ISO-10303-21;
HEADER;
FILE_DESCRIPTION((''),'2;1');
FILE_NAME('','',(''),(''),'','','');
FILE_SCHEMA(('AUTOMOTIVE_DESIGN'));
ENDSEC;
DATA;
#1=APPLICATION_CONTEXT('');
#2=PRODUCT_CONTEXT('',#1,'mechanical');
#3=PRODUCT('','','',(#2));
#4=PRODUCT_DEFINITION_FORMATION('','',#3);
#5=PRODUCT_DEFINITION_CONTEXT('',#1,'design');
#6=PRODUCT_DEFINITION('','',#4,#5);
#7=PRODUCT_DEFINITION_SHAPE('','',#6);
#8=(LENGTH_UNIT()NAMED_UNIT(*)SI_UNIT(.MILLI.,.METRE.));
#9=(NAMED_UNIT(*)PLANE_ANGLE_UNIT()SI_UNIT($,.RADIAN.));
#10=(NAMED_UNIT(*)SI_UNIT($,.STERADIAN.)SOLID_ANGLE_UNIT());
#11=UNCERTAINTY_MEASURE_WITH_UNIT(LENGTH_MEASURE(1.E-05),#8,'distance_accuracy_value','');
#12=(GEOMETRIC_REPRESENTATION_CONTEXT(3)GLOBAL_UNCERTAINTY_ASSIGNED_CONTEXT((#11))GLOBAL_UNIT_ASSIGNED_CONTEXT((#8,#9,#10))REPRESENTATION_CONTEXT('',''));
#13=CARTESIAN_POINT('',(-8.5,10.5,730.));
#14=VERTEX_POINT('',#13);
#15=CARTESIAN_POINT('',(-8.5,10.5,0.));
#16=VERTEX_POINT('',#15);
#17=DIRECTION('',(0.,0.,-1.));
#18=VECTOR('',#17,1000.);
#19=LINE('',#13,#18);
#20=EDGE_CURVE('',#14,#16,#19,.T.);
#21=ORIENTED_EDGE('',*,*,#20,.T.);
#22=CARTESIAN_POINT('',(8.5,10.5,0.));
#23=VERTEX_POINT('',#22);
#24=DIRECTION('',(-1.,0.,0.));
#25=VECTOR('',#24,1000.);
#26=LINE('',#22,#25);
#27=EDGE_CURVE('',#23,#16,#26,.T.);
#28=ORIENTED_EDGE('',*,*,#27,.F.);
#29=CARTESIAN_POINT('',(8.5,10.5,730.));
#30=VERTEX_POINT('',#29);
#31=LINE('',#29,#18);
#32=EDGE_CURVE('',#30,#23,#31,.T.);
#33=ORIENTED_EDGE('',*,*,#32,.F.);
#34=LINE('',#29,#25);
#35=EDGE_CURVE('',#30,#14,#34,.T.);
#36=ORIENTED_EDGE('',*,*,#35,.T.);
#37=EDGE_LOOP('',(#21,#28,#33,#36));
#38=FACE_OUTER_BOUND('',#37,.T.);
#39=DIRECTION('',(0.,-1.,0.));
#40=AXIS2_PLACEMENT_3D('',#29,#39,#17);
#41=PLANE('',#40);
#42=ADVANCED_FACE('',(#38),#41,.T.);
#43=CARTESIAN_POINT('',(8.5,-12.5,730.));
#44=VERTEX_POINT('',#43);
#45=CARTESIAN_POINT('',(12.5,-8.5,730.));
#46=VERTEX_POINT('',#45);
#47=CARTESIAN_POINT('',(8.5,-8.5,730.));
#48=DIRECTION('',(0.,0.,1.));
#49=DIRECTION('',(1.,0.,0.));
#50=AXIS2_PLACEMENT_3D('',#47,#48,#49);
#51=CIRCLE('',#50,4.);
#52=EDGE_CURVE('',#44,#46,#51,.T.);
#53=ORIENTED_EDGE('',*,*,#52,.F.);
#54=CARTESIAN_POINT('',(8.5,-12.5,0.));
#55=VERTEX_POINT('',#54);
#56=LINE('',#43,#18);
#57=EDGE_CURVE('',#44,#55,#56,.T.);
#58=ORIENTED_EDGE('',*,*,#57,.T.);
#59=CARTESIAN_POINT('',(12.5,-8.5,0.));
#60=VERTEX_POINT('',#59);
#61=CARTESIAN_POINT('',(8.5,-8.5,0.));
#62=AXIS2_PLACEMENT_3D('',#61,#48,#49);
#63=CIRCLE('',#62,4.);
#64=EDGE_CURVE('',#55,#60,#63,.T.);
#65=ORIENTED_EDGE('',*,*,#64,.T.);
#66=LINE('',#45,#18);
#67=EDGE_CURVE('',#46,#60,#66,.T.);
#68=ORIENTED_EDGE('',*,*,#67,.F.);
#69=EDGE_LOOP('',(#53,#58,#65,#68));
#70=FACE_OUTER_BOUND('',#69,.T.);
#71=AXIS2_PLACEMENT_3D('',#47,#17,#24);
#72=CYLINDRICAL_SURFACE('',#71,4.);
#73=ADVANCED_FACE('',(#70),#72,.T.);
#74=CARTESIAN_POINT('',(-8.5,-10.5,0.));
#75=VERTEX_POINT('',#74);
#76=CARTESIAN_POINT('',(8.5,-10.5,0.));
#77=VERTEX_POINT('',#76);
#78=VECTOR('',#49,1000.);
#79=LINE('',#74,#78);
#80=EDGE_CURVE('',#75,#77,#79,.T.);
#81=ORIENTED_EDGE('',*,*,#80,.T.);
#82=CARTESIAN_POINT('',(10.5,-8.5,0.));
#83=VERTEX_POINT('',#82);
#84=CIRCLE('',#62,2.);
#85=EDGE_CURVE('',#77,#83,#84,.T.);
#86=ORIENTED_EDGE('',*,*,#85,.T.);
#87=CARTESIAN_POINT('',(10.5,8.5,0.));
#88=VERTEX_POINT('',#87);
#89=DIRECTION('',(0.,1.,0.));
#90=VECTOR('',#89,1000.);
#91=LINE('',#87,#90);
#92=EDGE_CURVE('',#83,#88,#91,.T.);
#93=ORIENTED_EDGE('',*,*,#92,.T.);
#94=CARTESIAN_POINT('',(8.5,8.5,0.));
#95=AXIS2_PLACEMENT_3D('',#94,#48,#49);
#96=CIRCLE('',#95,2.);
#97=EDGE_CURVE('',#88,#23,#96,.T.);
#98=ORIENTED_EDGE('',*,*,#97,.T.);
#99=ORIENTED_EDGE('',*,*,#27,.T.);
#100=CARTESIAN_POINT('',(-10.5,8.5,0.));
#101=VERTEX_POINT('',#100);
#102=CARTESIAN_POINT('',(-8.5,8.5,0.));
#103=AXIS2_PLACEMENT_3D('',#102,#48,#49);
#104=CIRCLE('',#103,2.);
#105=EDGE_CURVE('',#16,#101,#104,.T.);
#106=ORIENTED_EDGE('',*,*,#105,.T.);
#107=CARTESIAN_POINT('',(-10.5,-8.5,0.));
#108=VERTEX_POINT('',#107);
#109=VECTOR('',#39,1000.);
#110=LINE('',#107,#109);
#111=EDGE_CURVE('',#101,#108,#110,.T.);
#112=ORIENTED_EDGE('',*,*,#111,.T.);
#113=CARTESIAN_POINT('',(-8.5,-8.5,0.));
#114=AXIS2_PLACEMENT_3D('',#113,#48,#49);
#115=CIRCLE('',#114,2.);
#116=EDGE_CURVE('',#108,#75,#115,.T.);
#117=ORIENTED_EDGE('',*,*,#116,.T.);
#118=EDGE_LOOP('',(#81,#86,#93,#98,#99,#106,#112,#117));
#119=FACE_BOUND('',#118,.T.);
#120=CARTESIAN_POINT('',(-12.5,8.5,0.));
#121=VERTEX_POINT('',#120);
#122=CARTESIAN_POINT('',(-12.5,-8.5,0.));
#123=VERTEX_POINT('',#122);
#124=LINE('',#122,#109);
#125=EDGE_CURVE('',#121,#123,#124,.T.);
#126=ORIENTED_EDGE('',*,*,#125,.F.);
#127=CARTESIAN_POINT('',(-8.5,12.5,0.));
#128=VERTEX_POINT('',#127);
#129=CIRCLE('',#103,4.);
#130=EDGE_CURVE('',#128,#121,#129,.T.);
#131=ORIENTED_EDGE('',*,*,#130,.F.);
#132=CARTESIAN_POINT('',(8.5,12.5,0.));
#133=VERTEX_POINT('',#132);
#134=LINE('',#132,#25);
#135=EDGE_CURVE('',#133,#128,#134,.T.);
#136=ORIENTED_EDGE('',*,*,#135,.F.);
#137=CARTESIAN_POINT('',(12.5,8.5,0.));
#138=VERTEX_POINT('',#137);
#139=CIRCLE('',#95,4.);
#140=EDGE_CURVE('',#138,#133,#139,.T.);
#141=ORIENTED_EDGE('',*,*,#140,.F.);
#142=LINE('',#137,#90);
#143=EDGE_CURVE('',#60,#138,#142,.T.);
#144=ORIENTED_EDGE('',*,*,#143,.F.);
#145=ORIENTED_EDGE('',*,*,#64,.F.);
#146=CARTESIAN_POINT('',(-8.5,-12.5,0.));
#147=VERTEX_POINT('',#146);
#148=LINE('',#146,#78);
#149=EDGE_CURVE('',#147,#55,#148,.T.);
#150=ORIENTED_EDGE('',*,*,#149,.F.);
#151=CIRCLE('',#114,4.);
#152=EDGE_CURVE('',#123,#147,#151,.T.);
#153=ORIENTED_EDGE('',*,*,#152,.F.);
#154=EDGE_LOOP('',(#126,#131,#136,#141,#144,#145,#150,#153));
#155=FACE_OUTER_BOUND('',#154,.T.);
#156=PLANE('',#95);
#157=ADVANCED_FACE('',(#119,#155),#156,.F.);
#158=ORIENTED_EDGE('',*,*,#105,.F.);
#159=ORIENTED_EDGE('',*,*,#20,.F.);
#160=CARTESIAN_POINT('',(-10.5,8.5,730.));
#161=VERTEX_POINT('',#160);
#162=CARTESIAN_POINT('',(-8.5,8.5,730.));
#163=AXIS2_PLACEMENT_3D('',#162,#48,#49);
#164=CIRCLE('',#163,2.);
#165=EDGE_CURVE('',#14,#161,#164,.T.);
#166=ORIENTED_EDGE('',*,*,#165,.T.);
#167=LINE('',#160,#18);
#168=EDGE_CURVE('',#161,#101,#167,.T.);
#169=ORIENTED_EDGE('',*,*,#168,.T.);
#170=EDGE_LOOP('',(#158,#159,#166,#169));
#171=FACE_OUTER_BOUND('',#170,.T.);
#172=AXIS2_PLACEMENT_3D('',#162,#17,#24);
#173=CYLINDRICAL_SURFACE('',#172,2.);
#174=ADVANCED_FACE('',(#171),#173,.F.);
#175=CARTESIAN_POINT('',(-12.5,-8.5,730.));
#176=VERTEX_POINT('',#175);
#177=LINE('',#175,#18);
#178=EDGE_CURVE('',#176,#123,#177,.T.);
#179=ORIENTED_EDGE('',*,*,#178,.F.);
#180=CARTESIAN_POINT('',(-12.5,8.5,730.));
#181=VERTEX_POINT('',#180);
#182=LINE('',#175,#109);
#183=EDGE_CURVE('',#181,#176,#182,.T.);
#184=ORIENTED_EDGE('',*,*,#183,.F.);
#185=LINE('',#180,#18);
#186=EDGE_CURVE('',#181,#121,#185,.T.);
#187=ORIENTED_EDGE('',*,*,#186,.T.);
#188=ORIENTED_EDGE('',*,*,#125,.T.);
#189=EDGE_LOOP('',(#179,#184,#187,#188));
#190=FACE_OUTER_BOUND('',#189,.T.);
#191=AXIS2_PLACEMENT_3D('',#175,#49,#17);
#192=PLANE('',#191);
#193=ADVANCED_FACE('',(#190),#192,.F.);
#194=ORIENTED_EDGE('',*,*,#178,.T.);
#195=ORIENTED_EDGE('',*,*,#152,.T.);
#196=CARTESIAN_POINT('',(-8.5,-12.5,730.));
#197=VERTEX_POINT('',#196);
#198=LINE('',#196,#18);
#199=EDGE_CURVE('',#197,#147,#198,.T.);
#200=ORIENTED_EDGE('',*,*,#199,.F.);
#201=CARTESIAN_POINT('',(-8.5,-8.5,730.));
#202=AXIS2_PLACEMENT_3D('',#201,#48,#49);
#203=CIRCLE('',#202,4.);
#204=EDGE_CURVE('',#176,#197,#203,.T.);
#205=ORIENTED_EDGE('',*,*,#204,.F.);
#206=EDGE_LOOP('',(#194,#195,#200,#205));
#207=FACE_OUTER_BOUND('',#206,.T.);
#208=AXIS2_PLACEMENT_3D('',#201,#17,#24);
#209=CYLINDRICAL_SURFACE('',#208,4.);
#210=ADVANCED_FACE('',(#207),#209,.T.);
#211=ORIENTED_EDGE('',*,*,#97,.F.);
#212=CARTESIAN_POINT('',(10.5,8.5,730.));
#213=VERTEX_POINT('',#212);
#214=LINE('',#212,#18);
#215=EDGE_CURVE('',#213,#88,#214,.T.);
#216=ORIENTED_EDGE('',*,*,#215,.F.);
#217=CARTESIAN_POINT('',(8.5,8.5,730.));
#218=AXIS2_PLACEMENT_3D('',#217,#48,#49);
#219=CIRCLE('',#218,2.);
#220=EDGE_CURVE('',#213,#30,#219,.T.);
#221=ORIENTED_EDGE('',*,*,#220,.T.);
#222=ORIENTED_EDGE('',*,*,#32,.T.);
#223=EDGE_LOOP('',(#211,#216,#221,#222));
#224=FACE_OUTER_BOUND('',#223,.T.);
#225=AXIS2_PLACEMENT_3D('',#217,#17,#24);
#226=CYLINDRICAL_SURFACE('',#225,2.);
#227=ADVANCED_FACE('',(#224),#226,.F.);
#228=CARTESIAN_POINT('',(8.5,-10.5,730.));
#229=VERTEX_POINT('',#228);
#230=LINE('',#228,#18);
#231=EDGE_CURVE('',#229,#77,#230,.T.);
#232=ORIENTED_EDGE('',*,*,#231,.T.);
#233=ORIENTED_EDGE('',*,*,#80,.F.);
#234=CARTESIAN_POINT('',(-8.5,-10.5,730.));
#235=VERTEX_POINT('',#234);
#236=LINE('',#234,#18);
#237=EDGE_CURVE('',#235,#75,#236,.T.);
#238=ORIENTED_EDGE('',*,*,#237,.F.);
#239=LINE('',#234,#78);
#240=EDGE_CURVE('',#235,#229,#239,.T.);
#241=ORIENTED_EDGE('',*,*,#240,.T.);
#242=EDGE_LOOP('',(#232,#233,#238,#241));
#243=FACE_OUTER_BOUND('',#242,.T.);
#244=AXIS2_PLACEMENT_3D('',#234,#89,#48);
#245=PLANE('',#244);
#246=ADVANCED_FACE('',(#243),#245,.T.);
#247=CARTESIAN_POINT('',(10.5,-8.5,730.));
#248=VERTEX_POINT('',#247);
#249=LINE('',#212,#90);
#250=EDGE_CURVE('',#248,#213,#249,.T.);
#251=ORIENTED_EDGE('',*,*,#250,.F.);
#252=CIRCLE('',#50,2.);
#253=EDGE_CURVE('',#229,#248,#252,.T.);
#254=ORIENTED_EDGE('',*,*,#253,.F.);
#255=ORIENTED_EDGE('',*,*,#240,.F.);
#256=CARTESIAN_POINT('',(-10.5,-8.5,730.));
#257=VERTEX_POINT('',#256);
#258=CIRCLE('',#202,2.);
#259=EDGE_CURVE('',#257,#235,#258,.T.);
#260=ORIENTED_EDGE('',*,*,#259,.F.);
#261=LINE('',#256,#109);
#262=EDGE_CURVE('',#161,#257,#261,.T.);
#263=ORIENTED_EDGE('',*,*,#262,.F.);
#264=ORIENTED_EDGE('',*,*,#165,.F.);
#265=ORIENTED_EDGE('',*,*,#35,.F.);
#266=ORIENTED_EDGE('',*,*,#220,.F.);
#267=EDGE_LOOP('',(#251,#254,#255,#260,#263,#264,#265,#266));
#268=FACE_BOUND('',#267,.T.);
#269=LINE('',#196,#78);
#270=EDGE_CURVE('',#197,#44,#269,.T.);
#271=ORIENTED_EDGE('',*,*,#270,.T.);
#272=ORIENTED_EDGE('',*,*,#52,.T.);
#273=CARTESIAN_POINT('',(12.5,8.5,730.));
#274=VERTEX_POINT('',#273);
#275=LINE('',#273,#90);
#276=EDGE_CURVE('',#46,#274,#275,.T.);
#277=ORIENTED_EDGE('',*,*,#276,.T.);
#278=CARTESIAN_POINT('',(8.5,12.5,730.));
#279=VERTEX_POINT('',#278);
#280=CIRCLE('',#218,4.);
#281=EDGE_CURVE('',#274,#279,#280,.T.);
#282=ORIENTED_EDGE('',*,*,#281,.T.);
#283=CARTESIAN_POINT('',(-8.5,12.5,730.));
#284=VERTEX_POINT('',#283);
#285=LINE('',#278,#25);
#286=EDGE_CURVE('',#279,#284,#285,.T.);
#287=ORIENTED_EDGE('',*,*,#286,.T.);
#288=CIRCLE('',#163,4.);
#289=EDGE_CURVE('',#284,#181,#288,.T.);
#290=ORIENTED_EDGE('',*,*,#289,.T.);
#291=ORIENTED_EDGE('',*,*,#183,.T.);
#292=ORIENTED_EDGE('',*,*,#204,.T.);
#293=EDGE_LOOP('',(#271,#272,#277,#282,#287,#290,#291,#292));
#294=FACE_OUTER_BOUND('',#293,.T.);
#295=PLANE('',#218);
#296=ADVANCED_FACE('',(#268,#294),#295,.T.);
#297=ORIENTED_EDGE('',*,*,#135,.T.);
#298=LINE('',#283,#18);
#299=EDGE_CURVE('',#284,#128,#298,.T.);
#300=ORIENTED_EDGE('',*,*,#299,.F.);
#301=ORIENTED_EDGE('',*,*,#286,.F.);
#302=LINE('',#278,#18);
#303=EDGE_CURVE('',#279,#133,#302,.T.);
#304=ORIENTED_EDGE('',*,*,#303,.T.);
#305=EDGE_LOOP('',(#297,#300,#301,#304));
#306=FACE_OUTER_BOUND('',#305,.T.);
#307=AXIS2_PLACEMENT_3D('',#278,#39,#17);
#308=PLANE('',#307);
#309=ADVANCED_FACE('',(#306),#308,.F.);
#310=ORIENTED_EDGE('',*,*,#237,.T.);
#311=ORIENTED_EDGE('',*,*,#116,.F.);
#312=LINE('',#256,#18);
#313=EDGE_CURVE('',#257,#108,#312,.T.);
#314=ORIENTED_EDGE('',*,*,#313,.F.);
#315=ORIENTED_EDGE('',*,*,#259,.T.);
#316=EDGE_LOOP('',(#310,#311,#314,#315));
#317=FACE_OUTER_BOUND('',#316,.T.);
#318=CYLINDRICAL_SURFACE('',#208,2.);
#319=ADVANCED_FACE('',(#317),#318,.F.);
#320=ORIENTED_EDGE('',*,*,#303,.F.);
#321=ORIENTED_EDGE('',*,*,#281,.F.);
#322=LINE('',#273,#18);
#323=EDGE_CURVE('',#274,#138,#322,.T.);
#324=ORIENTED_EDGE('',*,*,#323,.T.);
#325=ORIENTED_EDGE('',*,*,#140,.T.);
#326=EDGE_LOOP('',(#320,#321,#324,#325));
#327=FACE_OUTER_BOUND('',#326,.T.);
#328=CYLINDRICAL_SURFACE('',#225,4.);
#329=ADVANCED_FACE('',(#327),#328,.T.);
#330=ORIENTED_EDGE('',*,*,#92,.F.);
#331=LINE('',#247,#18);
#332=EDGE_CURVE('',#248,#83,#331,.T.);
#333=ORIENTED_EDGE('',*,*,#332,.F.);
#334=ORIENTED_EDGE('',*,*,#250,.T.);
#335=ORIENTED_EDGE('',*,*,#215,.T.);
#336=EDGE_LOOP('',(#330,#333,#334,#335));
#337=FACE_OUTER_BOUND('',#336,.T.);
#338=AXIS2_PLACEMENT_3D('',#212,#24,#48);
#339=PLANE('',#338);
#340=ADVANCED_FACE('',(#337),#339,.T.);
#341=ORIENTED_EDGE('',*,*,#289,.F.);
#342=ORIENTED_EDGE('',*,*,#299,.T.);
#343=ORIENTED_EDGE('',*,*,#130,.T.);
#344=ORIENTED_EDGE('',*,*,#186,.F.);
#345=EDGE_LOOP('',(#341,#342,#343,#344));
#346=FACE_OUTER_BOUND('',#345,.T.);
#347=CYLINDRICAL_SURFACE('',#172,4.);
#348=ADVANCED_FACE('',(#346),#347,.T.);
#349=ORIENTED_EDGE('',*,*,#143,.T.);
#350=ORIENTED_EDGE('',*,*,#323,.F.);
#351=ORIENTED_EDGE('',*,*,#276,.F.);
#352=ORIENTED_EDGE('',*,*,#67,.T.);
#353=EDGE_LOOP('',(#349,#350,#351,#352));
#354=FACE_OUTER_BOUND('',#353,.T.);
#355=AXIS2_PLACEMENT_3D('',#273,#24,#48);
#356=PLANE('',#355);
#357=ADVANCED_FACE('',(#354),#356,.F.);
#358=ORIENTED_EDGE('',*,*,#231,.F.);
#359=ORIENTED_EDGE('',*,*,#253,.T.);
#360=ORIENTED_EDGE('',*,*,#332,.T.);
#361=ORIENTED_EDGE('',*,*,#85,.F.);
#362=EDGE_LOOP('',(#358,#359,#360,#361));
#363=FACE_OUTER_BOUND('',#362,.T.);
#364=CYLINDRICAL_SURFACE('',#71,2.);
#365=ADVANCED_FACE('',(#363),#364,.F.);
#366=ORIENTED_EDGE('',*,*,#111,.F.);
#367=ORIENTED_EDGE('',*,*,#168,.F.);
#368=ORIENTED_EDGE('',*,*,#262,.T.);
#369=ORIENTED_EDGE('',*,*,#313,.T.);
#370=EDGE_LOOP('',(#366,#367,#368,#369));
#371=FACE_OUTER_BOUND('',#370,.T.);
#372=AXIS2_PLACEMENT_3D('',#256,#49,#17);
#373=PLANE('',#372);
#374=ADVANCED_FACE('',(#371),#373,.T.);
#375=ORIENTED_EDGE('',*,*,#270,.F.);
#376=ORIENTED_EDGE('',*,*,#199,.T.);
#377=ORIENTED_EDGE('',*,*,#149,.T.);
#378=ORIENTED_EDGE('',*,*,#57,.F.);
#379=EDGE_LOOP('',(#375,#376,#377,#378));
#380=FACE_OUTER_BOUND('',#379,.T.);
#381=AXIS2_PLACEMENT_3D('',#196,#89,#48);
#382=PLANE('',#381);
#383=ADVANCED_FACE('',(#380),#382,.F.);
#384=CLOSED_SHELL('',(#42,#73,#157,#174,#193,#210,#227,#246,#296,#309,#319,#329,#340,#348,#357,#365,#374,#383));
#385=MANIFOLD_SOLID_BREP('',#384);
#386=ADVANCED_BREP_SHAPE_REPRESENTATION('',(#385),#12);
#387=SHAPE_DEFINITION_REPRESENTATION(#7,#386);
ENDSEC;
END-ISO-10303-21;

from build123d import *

# Parameters (mm, degrees)
BOSS_EXTRUDE1_DEPTH = 730


with BuildPart() as part:
    # Sketch1 → Boss-Extrude1 (new body)
    with BuildSketch(Plane.XY):
        with BuildLine():
            Line((-8.5, -12.5), (8.5, -12.5))
            ThreePointArc((8.5, -12.5), (11.328427125, -11.328427125), (12.5, -8.5))
            Line((12.5, -8.5), (12.5, 8.5))
            ThreePointArc((12.5, 8.5), (11.328427125, 11.328427125), (8.5, 12.5))
            Line((8.5, 12.5), (-8.5, 12.5))
            ThreePointArc((-8.5, 12.5), (-11.328427125, 11.328427125), (-12.5, 8.5))
            Line((-12.5, 8.5), (-12.5, -8.5))
            ThreePointArc((-12.5, -8.5), (-11.328427125, -11.328427125), (-8.5, -12.5))
        make_face()
        with BuildLine():
            Line((-8.5, -10.5), (8.5, -10.5))
            ThreePointArc((8.5, -10.5), (9.914213562, -9.914213562), (10.5, -8.5))
            Line((10.5, -8.5), (10.5, 8.5))
            ThreePointArc((10.5, 8.5), (9.914213562, 9.914213562), (8.5, 10.5))
            Line((8.5, 10.5), (-8.5, 10.5))
            ThreePointArc((-8.5, 10.5), (-9.914213562, 9.914213562), (-10.5, 8.5))
            Line((-10.5, 8.5), (-10.5, -8.5))
            ThreePointArc((-10.5, -8.5), (-9.914213562, -9.914213562), (-8.5, -10.5))
        make_face(mode=Mode.SUBTRACT)
    extrude(amount=BOSS_EXTRUDE1_DEPTH)


solid = part.part
